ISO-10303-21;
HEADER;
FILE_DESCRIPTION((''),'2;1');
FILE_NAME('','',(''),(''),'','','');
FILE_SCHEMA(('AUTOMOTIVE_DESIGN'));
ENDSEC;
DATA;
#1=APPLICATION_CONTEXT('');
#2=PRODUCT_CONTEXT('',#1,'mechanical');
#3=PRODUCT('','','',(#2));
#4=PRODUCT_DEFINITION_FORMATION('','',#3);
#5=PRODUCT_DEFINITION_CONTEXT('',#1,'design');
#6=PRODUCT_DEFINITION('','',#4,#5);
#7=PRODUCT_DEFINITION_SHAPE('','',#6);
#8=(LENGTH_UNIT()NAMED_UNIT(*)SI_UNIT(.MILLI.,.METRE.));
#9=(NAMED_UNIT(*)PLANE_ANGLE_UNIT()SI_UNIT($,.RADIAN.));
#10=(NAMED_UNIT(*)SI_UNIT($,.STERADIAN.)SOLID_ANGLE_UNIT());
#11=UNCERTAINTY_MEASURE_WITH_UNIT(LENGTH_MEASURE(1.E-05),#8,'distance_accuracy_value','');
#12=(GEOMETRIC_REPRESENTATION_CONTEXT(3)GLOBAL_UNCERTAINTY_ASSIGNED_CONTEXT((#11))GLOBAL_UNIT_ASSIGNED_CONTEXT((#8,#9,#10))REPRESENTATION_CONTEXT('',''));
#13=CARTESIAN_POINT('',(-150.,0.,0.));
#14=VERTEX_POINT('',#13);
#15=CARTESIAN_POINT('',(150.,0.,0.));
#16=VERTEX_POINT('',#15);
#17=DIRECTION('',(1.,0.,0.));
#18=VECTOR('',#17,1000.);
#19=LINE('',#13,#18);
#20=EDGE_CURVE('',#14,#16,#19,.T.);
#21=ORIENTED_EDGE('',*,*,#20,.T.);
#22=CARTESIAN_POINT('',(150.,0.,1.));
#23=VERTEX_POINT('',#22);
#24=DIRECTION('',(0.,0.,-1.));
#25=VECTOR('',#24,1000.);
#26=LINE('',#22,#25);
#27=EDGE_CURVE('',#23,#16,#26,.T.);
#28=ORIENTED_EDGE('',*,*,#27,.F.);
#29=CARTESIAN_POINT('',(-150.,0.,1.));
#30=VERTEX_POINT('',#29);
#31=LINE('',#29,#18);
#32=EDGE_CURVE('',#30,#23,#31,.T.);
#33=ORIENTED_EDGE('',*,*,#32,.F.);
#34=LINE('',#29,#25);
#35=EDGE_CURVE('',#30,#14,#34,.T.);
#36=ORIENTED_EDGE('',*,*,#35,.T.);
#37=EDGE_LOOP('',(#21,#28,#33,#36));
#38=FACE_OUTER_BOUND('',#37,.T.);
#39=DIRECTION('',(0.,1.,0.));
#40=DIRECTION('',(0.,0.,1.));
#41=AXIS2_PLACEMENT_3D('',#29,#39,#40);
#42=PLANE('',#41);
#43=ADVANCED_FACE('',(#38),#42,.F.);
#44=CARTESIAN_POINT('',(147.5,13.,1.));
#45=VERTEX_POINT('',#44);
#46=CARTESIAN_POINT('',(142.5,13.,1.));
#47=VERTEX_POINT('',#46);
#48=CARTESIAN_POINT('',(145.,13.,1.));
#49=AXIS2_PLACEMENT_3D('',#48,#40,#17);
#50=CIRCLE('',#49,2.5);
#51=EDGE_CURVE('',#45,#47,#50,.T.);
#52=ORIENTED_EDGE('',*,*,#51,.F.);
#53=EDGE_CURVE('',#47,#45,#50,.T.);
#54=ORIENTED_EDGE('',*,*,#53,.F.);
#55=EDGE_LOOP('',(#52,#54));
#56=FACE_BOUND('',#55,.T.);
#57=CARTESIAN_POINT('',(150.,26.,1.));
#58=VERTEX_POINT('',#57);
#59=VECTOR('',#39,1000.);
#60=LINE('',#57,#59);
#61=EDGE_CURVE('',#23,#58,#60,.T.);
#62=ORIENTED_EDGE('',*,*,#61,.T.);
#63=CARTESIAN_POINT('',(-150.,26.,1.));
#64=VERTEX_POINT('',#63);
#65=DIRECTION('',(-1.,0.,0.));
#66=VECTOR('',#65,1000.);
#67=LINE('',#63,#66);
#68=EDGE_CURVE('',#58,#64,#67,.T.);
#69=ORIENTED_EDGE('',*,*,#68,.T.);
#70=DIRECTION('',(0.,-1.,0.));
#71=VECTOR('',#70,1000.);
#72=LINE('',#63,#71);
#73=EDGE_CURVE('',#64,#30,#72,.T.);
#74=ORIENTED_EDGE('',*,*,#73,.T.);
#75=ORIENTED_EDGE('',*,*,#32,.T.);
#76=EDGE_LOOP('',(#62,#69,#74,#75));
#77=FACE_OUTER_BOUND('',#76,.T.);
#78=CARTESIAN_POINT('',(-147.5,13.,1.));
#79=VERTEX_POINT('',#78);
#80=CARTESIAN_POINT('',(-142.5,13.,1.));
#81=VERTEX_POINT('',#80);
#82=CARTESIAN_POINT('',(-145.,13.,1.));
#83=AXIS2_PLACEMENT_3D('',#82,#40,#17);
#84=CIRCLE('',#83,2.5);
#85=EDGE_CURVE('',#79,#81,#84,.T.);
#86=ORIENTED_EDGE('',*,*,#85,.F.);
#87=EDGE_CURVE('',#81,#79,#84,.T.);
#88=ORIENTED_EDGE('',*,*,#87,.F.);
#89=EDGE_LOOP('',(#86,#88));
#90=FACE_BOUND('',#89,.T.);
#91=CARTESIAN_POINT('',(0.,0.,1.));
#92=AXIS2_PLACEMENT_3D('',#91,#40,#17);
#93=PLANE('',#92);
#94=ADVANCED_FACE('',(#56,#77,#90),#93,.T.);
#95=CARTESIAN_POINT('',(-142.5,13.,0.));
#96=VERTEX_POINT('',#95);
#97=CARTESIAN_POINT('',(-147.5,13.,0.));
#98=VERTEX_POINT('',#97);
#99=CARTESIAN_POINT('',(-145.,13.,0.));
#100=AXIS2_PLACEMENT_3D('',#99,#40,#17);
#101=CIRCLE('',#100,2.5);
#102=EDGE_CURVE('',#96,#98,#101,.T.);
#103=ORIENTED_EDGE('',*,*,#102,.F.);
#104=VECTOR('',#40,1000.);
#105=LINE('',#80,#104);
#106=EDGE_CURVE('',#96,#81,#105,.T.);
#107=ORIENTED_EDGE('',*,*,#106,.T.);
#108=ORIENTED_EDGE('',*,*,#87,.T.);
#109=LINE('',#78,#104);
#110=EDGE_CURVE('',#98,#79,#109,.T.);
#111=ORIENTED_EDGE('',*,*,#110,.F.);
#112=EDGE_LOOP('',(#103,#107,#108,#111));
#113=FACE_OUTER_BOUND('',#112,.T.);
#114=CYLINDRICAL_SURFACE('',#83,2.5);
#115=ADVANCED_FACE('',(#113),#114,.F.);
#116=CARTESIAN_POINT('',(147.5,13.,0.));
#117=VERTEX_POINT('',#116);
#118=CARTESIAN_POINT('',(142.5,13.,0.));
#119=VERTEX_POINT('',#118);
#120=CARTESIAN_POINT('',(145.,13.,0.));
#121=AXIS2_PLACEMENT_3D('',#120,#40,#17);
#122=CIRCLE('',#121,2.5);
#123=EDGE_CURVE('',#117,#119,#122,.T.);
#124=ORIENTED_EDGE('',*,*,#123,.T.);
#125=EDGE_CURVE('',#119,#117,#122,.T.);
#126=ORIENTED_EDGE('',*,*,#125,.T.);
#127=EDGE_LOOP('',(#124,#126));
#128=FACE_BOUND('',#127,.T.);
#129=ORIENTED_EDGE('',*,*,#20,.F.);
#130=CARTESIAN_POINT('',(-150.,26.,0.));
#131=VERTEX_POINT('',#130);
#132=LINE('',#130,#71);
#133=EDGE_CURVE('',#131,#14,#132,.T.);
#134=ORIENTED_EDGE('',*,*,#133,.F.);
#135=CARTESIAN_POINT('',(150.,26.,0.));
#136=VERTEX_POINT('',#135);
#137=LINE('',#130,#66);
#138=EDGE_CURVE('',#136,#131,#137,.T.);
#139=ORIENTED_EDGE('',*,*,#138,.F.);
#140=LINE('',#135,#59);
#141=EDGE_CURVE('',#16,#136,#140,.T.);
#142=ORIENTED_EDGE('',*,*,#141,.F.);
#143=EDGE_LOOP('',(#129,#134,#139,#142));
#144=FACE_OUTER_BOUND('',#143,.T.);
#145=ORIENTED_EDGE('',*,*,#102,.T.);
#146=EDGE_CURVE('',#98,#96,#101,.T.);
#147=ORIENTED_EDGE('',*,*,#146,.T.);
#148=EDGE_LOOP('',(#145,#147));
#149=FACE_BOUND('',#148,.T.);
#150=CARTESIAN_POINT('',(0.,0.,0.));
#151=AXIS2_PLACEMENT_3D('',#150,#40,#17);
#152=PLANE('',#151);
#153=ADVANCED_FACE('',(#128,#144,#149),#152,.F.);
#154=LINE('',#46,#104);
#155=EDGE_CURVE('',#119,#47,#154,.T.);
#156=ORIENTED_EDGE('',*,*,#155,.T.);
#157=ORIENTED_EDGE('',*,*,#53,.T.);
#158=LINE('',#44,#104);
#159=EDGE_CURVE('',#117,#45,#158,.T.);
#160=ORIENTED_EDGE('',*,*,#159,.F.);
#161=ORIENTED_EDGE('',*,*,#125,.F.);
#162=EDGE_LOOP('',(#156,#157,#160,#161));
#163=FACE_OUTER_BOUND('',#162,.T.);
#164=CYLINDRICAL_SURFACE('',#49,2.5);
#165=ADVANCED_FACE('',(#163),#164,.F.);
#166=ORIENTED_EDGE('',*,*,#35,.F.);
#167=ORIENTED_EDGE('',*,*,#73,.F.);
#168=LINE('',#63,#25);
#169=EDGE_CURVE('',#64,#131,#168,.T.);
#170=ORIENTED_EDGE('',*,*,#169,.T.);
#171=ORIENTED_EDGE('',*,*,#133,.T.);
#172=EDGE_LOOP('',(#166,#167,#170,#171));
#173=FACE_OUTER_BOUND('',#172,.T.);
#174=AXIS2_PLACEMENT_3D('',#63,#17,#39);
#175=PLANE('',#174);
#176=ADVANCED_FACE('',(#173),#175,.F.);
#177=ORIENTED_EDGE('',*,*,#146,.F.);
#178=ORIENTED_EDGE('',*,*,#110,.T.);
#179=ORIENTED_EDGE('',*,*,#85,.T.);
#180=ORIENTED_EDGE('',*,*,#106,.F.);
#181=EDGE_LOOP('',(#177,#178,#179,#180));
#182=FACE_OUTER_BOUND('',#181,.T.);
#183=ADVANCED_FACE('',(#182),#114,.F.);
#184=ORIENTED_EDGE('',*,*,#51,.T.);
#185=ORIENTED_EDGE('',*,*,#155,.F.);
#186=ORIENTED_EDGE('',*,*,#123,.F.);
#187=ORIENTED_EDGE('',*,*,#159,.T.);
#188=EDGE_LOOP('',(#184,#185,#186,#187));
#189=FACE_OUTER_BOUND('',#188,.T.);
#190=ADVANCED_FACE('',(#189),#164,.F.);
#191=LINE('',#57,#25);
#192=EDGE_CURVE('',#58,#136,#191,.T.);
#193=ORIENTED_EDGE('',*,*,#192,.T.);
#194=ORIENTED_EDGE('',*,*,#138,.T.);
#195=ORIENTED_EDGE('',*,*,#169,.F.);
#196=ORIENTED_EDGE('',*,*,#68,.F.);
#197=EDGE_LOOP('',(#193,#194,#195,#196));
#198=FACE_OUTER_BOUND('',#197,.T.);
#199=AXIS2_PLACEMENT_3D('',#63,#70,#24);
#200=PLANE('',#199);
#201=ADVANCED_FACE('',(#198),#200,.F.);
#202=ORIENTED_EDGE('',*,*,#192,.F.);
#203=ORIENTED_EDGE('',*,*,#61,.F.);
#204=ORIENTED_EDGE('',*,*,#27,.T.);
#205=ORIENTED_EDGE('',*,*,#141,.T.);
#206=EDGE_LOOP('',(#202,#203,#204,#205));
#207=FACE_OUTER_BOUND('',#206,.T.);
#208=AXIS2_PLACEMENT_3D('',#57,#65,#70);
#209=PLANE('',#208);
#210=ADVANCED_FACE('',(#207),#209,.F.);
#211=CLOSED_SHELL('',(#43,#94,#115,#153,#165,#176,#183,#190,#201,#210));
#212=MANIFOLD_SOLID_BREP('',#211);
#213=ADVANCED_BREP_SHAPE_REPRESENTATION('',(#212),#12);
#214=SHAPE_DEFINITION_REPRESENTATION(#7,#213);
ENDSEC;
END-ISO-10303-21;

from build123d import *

# Parameters (mm, degrees)
SKETCH_1_W                = 300
SKETCH_1_H                = 26
EXTRUDE_1_DEPTH           = 1
HOLE_WIZARD_5_0_5_1_D     = 5
HOLE_WIZARD_5_0_5_1_DEPTH = 5
HOLE_WIZARD_5_0_5_1_TIP   = 1.502151548


with BuildPart() as part:
    # 草图1 → 凸台-拉伸1 (new body)
    with BuildSketch(Plane.XY):
        with Locations((0, 13)):
            Rectangle(SKETCH_1_W, SKETCH_1_H)
    extrude(amount=EXTRUDE_1_DEPTH)

    # Ø5.0 (5) 直径孔1
    with Locations(Plane.XY.offset(1)):
        with Locations((-145, 13), (145, 13)):
            Hole(HOLE_WIZARD_5_0_5_1_D / 2, depth=HOLE_WIZARD_5_0_5_1_DEPTH)
            with Locations((0, 0, -(HOLE_WIZARD_5_0_5_1_DEPTH + HOLE_WIZARD_5_0_5_1_TIP / 2))):  # 118° drill point
                Cone(0, HOLE_WIZARD_5_0_5_1_D / 2, HOLE_WIZARD_5_0_5_1_TIP, mode=Mode.SUBTRACT)


solid = part.part
